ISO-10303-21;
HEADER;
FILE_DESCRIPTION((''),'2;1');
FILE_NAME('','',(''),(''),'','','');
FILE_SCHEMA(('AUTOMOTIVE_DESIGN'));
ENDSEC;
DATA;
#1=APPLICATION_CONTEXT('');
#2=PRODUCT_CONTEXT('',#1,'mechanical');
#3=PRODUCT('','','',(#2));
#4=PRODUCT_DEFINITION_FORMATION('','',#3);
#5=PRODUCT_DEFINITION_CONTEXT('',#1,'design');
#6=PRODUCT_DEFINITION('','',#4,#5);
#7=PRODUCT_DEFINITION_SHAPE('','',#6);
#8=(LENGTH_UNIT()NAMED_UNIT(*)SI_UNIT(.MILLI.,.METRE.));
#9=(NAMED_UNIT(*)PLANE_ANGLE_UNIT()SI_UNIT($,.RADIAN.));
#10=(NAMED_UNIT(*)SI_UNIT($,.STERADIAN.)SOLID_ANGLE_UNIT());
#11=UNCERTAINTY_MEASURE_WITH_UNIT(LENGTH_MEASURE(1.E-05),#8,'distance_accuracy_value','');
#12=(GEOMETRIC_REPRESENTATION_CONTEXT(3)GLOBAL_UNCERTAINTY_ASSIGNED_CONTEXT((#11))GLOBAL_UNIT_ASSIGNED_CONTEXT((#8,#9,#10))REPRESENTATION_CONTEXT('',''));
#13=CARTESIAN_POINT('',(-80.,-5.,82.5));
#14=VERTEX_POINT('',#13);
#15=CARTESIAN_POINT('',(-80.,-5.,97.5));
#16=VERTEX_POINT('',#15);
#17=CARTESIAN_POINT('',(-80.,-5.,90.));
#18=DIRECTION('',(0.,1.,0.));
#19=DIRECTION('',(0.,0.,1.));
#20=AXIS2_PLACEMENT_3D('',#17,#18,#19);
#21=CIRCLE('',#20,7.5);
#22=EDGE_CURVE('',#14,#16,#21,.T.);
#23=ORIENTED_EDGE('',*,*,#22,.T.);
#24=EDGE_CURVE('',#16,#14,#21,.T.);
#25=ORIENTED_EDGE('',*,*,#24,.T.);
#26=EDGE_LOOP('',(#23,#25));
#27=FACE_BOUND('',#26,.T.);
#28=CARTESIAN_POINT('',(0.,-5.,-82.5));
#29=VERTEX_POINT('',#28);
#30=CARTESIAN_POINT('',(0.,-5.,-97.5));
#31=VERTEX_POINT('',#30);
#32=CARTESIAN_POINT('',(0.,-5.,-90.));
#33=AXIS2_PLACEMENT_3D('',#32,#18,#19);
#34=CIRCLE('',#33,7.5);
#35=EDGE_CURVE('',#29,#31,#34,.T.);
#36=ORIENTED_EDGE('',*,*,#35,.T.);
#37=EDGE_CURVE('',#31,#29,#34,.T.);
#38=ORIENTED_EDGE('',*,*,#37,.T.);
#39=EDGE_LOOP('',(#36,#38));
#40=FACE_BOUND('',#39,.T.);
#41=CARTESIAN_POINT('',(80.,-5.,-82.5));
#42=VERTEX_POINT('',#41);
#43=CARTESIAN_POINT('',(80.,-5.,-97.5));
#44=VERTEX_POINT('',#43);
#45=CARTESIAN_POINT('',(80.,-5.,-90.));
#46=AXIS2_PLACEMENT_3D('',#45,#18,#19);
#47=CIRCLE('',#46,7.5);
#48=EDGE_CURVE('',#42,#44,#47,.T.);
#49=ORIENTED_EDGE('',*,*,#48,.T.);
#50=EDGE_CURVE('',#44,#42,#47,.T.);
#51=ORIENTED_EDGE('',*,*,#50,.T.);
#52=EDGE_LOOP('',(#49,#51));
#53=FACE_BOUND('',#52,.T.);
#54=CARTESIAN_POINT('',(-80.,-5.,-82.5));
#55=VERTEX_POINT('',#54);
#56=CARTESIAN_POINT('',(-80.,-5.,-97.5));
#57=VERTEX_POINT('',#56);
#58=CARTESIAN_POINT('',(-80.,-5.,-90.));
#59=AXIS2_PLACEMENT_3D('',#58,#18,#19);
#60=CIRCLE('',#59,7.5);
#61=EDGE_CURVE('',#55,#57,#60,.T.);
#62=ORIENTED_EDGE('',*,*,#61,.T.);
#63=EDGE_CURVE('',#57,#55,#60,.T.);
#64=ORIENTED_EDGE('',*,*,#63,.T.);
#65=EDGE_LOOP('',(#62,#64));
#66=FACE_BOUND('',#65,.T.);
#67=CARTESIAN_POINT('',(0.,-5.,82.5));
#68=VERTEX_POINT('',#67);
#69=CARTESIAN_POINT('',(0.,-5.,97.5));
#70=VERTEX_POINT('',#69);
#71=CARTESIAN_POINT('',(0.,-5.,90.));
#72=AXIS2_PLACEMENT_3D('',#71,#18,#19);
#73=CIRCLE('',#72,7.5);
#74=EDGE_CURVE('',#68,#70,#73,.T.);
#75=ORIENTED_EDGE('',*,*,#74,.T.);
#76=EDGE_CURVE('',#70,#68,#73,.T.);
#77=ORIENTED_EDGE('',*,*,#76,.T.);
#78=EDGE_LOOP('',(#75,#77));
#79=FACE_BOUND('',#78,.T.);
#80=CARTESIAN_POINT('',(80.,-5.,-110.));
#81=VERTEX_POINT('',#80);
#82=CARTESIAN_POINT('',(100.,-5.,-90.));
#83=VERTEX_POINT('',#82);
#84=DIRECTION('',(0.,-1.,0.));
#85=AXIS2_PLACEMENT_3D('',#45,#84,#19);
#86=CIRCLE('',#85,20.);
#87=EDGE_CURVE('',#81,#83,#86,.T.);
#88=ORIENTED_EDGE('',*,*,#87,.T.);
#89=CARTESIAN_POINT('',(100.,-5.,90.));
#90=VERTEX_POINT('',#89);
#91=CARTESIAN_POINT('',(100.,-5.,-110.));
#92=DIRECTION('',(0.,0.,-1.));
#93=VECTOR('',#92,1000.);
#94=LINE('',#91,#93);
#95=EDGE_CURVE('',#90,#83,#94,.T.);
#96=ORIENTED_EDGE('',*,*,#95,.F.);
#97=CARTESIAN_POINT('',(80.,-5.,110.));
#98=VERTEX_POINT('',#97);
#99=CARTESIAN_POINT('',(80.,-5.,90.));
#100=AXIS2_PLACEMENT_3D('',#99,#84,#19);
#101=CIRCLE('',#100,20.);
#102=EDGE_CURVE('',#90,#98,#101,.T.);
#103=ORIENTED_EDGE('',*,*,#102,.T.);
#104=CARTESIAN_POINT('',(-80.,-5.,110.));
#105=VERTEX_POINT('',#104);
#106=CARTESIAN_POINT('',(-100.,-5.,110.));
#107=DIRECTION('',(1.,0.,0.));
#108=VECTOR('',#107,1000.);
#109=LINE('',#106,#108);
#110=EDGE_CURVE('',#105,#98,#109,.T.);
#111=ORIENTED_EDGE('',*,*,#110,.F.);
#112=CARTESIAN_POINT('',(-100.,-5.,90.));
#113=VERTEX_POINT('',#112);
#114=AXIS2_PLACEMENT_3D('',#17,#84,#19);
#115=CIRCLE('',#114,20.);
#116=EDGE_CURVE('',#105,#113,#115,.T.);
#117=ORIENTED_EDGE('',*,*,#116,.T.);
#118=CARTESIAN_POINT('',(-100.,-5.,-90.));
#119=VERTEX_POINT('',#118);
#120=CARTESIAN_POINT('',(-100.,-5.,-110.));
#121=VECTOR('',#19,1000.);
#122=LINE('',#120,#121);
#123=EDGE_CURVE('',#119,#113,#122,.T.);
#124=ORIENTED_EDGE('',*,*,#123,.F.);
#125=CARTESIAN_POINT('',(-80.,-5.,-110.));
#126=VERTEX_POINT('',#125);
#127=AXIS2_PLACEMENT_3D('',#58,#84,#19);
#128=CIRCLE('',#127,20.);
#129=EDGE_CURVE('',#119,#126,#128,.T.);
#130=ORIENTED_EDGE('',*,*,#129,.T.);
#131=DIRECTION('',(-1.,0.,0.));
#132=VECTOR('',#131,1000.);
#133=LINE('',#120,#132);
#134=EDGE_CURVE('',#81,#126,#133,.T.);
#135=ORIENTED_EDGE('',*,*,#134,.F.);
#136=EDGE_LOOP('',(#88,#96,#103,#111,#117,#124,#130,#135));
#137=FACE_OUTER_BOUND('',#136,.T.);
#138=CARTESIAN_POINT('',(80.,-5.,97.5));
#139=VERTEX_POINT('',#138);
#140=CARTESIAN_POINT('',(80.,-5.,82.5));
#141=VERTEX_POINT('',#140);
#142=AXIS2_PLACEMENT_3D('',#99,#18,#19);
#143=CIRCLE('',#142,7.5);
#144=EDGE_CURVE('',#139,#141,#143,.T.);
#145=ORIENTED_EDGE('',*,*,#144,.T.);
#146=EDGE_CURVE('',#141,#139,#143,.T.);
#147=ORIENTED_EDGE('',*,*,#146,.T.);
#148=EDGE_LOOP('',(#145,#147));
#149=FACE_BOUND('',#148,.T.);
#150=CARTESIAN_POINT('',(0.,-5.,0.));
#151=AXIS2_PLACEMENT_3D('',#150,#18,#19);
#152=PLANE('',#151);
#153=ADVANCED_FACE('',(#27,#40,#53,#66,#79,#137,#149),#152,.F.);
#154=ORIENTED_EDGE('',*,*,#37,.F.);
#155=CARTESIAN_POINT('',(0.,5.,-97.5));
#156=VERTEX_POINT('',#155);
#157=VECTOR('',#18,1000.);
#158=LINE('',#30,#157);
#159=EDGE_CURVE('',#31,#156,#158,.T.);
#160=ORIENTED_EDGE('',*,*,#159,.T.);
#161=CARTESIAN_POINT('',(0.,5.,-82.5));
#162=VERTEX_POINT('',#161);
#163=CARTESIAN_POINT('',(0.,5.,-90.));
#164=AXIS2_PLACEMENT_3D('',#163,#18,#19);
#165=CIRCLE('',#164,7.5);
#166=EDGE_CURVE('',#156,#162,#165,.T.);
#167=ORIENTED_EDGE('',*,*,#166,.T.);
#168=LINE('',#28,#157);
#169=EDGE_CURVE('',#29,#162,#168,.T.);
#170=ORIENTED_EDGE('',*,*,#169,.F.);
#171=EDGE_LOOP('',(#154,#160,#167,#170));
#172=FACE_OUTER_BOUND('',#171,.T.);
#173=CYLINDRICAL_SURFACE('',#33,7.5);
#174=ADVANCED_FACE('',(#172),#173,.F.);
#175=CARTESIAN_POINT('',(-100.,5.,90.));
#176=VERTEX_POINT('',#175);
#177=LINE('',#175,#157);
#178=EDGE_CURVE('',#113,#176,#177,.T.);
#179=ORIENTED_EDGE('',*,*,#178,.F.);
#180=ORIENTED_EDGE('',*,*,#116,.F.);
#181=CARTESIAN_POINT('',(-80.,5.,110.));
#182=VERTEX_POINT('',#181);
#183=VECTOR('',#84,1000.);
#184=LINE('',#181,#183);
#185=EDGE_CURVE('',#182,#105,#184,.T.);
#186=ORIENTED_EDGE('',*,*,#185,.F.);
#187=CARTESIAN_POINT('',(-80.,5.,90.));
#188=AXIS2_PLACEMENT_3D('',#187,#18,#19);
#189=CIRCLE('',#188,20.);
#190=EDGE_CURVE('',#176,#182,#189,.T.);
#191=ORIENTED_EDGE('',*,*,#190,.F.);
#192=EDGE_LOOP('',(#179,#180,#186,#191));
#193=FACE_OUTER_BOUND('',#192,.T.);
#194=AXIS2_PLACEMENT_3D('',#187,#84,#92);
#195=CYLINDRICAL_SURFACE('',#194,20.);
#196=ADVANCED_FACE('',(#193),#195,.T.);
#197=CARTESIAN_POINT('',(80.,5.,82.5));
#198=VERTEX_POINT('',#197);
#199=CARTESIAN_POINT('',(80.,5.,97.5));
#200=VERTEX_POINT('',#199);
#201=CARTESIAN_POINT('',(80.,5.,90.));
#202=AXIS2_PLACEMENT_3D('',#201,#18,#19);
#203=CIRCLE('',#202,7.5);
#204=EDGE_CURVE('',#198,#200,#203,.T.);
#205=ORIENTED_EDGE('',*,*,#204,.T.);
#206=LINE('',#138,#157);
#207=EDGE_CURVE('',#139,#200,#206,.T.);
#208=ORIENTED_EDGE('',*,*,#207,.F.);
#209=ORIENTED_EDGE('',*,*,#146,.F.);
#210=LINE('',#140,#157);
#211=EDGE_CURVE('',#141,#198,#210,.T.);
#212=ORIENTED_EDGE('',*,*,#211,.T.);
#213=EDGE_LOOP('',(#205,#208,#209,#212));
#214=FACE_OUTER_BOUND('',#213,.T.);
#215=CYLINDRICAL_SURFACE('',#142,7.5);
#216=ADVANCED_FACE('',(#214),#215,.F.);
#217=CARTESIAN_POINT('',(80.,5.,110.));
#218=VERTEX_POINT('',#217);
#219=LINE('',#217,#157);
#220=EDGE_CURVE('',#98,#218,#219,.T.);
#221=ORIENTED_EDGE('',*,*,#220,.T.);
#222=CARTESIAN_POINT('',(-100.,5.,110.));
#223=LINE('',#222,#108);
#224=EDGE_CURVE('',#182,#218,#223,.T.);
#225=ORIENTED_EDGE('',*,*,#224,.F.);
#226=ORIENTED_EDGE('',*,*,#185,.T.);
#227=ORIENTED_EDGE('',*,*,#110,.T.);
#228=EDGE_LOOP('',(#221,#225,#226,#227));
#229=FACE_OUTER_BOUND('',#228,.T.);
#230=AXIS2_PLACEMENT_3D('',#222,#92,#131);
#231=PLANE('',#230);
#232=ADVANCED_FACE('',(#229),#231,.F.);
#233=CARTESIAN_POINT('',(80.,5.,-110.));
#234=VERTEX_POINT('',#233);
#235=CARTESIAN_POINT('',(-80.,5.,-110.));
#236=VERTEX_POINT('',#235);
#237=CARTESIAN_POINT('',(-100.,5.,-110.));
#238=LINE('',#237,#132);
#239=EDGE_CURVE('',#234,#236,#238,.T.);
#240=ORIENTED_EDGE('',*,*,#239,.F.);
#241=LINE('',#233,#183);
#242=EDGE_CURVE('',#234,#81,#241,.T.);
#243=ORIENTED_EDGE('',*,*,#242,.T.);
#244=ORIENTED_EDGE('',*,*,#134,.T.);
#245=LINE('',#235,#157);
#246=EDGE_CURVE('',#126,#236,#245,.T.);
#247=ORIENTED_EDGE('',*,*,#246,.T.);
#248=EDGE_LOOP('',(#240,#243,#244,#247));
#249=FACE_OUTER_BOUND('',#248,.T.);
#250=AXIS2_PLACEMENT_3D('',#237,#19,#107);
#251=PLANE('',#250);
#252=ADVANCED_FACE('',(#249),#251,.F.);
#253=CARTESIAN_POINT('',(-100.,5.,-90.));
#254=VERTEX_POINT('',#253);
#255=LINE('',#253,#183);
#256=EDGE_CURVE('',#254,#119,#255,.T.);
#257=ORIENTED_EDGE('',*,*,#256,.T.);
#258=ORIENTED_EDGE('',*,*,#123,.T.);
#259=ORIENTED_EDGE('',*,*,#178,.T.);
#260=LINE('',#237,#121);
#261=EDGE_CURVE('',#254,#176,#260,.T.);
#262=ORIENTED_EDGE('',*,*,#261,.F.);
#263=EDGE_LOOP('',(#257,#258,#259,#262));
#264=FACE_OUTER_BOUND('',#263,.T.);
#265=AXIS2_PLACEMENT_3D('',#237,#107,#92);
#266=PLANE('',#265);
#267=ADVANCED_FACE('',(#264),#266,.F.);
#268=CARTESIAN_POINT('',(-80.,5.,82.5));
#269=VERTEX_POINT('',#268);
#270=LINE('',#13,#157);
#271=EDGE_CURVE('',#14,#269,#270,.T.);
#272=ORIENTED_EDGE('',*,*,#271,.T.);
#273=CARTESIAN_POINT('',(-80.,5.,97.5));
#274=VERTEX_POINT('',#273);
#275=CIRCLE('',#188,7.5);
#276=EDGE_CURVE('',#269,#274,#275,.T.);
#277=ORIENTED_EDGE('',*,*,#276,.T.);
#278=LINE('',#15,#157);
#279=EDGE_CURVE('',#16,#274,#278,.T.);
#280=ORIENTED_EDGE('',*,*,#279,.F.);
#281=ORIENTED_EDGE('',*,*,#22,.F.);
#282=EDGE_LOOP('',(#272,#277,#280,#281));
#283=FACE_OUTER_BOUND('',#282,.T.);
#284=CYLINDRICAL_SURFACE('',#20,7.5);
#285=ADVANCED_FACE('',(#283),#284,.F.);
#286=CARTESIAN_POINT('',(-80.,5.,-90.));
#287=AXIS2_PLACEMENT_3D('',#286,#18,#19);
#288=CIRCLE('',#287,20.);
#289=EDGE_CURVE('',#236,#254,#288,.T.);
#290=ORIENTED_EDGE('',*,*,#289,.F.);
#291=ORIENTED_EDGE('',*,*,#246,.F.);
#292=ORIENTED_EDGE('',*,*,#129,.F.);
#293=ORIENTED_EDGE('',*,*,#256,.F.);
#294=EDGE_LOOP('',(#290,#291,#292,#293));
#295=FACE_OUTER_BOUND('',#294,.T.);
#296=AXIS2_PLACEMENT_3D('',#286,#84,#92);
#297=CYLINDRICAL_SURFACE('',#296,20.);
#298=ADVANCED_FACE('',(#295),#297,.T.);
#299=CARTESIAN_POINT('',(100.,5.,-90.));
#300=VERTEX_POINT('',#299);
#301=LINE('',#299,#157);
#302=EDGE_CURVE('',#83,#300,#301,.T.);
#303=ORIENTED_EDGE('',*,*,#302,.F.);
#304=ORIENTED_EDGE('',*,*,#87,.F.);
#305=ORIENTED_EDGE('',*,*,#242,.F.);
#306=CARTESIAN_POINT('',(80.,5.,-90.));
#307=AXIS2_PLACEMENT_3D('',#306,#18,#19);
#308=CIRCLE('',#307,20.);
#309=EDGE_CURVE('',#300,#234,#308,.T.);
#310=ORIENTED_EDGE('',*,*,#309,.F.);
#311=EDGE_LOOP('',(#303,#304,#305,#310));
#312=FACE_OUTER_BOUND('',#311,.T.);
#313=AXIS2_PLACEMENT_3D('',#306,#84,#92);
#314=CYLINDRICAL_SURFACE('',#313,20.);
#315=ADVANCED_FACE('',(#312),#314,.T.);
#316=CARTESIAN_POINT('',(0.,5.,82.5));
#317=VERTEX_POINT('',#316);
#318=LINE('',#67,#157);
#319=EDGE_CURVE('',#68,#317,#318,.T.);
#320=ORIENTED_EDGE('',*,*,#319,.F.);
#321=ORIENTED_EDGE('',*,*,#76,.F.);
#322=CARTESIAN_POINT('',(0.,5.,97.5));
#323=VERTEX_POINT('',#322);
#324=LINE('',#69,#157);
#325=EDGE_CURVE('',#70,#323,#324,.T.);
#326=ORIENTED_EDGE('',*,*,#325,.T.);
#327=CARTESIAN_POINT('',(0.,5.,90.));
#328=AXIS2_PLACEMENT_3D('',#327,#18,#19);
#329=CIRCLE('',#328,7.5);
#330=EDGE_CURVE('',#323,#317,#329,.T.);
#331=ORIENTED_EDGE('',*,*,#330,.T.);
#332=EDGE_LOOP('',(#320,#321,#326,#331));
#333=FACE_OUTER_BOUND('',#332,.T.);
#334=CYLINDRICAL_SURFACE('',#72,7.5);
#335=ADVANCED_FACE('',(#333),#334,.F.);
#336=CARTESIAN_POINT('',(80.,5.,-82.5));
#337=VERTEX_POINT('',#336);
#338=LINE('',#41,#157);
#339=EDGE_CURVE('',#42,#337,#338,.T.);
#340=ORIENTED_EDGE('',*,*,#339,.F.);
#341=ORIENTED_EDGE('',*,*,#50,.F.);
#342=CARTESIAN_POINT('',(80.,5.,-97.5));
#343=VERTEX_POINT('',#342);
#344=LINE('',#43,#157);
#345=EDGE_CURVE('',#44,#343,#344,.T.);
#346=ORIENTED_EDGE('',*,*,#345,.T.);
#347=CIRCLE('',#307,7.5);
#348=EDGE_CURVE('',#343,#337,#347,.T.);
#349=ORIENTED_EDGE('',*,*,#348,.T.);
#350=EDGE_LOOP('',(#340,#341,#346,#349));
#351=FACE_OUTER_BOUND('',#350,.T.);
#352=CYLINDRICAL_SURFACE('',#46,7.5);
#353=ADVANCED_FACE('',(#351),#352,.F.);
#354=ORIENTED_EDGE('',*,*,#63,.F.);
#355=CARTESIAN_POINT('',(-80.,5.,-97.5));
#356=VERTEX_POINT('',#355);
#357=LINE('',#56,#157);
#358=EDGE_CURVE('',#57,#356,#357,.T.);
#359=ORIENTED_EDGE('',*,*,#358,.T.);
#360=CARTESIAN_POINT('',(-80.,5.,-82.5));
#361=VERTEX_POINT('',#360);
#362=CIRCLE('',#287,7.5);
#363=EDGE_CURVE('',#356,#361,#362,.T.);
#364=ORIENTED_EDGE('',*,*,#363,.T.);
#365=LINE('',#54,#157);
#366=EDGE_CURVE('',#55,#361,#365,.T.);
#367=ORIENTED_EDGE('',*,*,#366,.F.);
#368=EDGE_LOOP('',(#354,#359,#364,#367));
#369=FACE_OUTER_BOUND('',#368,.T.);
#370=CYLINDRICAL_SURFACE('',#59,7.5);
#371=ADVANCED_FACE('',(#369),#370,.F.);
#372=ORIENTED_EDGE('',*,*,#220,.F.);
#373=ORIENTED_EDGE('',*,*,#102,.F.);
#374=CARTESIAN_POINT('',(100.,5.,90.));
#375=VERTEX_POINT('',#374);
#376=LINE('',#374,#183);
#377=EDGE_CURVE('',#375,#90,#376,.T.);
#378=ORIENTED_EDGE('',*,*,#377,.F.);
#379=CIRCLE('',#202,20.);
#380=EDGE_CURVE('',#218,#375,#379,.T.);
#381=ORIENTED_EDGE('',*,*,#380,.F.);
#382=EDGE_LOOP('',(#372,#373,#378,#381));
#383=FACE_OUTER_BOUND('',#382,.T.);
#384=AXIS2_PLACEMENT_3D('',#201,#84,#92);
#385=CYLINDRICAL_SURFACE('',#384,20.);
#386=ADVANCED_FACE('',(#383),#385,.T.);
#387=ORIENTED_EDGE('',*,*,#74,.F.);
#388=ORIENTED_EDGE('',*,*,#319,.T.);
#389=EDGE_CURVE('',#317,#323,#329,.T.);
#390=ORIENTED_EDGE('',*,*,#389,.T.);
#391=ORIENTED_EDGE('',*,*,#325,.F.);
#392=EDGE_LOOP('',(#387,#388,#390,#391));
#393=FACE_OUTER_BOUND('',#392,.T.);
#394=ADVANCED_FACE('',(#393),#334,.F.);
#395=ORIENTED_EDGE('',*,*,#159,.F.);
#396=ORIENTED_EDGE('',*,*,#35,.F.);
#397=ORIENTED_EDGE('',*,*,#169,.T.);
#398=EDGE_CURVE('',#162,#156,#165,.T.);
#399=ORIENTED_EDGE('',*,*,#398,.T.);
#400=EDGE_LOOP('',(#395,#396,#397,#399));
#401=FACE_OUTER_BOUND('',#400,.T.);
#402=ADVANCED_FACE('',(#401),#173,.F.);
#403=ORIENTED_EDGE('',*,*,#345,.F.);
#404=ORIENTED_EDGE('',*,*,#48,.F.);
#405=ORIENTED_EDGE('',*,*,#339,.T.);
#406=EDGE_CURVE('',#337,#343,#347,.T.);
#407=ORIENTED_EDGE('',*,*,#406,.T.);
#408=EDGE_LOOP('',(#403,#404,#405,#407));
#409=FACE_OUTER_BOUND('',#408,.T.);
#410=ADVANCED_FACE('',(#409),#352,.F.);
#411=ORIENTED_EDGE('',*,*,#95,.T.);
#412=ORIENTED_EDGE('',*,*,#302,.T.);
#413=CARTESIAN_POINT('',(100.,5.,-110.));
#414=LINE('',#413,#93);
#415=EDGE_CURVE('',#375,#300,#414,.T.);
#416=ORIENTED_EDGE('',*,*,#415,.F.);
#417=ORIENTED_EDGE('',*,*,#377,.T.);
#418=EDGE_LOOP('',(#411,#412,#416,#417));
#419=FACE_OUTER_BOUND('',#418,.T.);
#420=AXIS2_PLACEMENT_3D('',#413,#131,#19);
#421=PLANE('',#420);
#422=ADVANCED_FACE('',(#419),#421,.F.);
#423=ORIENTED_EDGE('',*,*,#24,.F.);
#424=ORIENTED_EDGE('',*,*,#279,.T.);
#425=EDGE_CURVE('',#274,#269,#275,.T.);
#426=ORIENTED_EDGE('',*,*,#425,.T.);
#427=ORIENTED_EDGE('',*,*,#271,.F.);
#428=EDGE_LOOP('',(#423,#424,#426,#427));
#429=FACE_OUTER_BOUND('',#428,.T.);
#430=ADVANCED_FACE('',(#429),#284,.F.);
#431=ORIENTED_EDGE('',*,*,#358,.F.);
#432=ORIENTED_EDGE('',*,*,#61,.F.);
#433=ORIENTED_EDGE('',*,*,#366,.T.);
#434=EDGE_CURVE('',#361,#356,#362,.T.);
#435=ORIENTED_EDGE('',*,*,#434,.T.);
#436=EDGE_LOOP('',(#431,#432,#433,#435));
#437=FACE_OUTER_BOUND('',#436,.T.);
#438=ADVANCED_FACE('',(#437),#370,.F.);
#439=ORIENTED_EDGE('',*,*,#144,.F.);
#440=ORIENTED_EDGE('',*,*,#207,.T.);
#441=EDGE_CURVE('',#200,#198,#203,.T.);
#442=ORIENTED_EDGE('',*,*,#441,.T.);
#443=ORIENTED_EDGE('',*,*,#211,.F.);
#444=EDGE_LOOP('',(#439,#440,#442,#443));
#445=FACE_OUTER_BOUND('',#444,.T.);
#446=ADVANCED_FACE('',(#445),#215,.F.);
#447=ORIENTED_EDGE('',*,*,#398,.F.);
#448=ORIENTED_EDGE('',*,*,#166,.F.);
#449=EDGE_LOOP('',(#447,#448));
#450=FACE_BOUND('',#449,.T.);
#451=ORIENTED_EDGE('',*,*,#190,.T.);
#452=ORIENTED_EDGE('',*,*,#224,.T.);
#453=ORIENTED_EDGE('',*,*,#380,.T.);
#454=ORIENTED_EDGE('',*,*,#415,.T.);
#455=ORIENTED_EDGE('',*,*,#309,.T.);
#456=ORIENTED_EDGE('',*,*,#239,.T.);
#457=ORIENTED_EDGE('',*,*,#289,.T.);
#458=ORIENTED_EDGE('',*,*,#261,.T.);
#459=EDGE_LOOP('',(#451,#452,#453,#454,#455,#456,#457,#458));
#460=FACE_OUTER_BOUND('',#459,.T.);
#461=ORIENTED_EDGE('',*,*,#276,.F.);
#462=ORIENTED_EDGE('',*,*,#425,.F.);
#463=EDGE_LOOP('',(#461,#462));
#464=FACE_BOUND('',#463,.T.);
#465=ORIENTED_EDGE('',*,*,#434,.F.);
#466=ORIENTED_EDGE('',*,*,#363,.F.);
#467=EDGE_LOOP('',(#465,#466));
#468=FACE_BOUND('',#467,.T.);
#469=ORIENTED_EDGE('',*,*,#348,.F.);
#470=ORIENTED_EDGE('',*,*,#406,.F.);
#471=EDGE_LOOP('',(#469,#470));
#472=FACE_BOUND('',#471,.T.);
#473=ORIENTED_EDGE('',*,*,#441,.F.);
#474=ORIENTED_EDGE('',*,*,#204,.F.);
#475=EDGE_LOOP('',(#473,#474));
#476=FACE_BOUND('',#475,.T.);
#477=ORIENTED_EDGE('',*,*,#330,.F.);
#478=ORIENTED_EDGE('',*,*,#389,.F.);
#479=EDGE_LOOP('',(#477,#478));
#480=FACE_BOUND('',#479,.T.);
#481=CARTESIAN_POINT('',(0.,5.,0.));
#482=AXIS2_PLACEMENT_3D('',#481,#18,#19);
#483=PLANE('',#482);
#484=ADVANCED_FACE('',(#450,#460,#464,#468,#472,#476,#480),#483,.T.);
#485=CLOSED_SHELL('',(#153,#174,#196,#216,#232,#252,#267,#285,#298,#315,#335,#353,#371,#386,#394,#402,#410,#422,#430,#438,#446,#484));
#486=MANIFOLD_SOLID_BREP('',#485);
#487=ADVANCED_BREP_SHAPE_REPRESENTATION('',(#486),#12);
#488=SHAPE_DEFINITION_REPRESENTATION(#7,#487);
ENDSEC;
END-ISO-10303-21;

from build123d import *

# Parameters (mm, degrees)
SKETCH1_W            = 200
SKETCH1_H            = 220
BOSS_EXTRUDE1_DEPTH  = 5
SKETCH2_R            = 7.5
CUT_EXTRUDE1_DEPTH   = 10
LPATTERN1_COUNT      = 2
LPATTERN1_PITCH      = 180
LPATTERN1_COUNT_DIR2 = 3
LPATTERN1_PITCH_DIR2 = 80
FILLET1_R            = 20


with BuildPart() as part:
    # Sketch1 → Boss-Extrude1 (new, symmetric)
    with BuildSketch(Plane(origin=(0, 0, 0), x_dir=(1, 0, 0), z_dir=(0, 1, 0))):
        Rectangle(SKETCH1_W, SKETCH1_H)
    extrude(amount=BOSS_EXTRUDE1_DEPTH, both=True)

    # Sketch2 → Cut-Extrude1 (cut)
    with BuildSketch(Plane(origin=(0, 5, 0), x_dir=(1, 0, 0), z_dir=(0, 1, 0))):
        with Locations(Location((80, 90, 0), (0, 0, 270))):
            Circle(SKETCH2_R)
    cut_extrude1 = extrude(amount=-CUT_EXTRUDE1_DEPTH, mode=Mode.SUBTRACT)

    # LPattern1: Cut-Extrude1 2 × 3
    with Locations(*[(-j * LPATTERN1_PITCH_DIR2, 0, i * LPATTERN1_PITCH) for i in range(LPATTERN1_COUNT) for j in range(LPATTERN1_COUNT_DIR2) if (i, j) != (0, 0)]):
        add(cut_extrude1, mode=Mode.SUBTRACT)

    # Fillet1
    fillet1_edges = [part.edges().sort_by_distance(p)[0] for p in [
        (100, 0, 110),
        (-100, 0, 110),
        (-100, 0, -110),
        (100, 0, -110),
    ]]
    fillet(fillet1_edges, radius=FILLET1_R)


solid = part.part
